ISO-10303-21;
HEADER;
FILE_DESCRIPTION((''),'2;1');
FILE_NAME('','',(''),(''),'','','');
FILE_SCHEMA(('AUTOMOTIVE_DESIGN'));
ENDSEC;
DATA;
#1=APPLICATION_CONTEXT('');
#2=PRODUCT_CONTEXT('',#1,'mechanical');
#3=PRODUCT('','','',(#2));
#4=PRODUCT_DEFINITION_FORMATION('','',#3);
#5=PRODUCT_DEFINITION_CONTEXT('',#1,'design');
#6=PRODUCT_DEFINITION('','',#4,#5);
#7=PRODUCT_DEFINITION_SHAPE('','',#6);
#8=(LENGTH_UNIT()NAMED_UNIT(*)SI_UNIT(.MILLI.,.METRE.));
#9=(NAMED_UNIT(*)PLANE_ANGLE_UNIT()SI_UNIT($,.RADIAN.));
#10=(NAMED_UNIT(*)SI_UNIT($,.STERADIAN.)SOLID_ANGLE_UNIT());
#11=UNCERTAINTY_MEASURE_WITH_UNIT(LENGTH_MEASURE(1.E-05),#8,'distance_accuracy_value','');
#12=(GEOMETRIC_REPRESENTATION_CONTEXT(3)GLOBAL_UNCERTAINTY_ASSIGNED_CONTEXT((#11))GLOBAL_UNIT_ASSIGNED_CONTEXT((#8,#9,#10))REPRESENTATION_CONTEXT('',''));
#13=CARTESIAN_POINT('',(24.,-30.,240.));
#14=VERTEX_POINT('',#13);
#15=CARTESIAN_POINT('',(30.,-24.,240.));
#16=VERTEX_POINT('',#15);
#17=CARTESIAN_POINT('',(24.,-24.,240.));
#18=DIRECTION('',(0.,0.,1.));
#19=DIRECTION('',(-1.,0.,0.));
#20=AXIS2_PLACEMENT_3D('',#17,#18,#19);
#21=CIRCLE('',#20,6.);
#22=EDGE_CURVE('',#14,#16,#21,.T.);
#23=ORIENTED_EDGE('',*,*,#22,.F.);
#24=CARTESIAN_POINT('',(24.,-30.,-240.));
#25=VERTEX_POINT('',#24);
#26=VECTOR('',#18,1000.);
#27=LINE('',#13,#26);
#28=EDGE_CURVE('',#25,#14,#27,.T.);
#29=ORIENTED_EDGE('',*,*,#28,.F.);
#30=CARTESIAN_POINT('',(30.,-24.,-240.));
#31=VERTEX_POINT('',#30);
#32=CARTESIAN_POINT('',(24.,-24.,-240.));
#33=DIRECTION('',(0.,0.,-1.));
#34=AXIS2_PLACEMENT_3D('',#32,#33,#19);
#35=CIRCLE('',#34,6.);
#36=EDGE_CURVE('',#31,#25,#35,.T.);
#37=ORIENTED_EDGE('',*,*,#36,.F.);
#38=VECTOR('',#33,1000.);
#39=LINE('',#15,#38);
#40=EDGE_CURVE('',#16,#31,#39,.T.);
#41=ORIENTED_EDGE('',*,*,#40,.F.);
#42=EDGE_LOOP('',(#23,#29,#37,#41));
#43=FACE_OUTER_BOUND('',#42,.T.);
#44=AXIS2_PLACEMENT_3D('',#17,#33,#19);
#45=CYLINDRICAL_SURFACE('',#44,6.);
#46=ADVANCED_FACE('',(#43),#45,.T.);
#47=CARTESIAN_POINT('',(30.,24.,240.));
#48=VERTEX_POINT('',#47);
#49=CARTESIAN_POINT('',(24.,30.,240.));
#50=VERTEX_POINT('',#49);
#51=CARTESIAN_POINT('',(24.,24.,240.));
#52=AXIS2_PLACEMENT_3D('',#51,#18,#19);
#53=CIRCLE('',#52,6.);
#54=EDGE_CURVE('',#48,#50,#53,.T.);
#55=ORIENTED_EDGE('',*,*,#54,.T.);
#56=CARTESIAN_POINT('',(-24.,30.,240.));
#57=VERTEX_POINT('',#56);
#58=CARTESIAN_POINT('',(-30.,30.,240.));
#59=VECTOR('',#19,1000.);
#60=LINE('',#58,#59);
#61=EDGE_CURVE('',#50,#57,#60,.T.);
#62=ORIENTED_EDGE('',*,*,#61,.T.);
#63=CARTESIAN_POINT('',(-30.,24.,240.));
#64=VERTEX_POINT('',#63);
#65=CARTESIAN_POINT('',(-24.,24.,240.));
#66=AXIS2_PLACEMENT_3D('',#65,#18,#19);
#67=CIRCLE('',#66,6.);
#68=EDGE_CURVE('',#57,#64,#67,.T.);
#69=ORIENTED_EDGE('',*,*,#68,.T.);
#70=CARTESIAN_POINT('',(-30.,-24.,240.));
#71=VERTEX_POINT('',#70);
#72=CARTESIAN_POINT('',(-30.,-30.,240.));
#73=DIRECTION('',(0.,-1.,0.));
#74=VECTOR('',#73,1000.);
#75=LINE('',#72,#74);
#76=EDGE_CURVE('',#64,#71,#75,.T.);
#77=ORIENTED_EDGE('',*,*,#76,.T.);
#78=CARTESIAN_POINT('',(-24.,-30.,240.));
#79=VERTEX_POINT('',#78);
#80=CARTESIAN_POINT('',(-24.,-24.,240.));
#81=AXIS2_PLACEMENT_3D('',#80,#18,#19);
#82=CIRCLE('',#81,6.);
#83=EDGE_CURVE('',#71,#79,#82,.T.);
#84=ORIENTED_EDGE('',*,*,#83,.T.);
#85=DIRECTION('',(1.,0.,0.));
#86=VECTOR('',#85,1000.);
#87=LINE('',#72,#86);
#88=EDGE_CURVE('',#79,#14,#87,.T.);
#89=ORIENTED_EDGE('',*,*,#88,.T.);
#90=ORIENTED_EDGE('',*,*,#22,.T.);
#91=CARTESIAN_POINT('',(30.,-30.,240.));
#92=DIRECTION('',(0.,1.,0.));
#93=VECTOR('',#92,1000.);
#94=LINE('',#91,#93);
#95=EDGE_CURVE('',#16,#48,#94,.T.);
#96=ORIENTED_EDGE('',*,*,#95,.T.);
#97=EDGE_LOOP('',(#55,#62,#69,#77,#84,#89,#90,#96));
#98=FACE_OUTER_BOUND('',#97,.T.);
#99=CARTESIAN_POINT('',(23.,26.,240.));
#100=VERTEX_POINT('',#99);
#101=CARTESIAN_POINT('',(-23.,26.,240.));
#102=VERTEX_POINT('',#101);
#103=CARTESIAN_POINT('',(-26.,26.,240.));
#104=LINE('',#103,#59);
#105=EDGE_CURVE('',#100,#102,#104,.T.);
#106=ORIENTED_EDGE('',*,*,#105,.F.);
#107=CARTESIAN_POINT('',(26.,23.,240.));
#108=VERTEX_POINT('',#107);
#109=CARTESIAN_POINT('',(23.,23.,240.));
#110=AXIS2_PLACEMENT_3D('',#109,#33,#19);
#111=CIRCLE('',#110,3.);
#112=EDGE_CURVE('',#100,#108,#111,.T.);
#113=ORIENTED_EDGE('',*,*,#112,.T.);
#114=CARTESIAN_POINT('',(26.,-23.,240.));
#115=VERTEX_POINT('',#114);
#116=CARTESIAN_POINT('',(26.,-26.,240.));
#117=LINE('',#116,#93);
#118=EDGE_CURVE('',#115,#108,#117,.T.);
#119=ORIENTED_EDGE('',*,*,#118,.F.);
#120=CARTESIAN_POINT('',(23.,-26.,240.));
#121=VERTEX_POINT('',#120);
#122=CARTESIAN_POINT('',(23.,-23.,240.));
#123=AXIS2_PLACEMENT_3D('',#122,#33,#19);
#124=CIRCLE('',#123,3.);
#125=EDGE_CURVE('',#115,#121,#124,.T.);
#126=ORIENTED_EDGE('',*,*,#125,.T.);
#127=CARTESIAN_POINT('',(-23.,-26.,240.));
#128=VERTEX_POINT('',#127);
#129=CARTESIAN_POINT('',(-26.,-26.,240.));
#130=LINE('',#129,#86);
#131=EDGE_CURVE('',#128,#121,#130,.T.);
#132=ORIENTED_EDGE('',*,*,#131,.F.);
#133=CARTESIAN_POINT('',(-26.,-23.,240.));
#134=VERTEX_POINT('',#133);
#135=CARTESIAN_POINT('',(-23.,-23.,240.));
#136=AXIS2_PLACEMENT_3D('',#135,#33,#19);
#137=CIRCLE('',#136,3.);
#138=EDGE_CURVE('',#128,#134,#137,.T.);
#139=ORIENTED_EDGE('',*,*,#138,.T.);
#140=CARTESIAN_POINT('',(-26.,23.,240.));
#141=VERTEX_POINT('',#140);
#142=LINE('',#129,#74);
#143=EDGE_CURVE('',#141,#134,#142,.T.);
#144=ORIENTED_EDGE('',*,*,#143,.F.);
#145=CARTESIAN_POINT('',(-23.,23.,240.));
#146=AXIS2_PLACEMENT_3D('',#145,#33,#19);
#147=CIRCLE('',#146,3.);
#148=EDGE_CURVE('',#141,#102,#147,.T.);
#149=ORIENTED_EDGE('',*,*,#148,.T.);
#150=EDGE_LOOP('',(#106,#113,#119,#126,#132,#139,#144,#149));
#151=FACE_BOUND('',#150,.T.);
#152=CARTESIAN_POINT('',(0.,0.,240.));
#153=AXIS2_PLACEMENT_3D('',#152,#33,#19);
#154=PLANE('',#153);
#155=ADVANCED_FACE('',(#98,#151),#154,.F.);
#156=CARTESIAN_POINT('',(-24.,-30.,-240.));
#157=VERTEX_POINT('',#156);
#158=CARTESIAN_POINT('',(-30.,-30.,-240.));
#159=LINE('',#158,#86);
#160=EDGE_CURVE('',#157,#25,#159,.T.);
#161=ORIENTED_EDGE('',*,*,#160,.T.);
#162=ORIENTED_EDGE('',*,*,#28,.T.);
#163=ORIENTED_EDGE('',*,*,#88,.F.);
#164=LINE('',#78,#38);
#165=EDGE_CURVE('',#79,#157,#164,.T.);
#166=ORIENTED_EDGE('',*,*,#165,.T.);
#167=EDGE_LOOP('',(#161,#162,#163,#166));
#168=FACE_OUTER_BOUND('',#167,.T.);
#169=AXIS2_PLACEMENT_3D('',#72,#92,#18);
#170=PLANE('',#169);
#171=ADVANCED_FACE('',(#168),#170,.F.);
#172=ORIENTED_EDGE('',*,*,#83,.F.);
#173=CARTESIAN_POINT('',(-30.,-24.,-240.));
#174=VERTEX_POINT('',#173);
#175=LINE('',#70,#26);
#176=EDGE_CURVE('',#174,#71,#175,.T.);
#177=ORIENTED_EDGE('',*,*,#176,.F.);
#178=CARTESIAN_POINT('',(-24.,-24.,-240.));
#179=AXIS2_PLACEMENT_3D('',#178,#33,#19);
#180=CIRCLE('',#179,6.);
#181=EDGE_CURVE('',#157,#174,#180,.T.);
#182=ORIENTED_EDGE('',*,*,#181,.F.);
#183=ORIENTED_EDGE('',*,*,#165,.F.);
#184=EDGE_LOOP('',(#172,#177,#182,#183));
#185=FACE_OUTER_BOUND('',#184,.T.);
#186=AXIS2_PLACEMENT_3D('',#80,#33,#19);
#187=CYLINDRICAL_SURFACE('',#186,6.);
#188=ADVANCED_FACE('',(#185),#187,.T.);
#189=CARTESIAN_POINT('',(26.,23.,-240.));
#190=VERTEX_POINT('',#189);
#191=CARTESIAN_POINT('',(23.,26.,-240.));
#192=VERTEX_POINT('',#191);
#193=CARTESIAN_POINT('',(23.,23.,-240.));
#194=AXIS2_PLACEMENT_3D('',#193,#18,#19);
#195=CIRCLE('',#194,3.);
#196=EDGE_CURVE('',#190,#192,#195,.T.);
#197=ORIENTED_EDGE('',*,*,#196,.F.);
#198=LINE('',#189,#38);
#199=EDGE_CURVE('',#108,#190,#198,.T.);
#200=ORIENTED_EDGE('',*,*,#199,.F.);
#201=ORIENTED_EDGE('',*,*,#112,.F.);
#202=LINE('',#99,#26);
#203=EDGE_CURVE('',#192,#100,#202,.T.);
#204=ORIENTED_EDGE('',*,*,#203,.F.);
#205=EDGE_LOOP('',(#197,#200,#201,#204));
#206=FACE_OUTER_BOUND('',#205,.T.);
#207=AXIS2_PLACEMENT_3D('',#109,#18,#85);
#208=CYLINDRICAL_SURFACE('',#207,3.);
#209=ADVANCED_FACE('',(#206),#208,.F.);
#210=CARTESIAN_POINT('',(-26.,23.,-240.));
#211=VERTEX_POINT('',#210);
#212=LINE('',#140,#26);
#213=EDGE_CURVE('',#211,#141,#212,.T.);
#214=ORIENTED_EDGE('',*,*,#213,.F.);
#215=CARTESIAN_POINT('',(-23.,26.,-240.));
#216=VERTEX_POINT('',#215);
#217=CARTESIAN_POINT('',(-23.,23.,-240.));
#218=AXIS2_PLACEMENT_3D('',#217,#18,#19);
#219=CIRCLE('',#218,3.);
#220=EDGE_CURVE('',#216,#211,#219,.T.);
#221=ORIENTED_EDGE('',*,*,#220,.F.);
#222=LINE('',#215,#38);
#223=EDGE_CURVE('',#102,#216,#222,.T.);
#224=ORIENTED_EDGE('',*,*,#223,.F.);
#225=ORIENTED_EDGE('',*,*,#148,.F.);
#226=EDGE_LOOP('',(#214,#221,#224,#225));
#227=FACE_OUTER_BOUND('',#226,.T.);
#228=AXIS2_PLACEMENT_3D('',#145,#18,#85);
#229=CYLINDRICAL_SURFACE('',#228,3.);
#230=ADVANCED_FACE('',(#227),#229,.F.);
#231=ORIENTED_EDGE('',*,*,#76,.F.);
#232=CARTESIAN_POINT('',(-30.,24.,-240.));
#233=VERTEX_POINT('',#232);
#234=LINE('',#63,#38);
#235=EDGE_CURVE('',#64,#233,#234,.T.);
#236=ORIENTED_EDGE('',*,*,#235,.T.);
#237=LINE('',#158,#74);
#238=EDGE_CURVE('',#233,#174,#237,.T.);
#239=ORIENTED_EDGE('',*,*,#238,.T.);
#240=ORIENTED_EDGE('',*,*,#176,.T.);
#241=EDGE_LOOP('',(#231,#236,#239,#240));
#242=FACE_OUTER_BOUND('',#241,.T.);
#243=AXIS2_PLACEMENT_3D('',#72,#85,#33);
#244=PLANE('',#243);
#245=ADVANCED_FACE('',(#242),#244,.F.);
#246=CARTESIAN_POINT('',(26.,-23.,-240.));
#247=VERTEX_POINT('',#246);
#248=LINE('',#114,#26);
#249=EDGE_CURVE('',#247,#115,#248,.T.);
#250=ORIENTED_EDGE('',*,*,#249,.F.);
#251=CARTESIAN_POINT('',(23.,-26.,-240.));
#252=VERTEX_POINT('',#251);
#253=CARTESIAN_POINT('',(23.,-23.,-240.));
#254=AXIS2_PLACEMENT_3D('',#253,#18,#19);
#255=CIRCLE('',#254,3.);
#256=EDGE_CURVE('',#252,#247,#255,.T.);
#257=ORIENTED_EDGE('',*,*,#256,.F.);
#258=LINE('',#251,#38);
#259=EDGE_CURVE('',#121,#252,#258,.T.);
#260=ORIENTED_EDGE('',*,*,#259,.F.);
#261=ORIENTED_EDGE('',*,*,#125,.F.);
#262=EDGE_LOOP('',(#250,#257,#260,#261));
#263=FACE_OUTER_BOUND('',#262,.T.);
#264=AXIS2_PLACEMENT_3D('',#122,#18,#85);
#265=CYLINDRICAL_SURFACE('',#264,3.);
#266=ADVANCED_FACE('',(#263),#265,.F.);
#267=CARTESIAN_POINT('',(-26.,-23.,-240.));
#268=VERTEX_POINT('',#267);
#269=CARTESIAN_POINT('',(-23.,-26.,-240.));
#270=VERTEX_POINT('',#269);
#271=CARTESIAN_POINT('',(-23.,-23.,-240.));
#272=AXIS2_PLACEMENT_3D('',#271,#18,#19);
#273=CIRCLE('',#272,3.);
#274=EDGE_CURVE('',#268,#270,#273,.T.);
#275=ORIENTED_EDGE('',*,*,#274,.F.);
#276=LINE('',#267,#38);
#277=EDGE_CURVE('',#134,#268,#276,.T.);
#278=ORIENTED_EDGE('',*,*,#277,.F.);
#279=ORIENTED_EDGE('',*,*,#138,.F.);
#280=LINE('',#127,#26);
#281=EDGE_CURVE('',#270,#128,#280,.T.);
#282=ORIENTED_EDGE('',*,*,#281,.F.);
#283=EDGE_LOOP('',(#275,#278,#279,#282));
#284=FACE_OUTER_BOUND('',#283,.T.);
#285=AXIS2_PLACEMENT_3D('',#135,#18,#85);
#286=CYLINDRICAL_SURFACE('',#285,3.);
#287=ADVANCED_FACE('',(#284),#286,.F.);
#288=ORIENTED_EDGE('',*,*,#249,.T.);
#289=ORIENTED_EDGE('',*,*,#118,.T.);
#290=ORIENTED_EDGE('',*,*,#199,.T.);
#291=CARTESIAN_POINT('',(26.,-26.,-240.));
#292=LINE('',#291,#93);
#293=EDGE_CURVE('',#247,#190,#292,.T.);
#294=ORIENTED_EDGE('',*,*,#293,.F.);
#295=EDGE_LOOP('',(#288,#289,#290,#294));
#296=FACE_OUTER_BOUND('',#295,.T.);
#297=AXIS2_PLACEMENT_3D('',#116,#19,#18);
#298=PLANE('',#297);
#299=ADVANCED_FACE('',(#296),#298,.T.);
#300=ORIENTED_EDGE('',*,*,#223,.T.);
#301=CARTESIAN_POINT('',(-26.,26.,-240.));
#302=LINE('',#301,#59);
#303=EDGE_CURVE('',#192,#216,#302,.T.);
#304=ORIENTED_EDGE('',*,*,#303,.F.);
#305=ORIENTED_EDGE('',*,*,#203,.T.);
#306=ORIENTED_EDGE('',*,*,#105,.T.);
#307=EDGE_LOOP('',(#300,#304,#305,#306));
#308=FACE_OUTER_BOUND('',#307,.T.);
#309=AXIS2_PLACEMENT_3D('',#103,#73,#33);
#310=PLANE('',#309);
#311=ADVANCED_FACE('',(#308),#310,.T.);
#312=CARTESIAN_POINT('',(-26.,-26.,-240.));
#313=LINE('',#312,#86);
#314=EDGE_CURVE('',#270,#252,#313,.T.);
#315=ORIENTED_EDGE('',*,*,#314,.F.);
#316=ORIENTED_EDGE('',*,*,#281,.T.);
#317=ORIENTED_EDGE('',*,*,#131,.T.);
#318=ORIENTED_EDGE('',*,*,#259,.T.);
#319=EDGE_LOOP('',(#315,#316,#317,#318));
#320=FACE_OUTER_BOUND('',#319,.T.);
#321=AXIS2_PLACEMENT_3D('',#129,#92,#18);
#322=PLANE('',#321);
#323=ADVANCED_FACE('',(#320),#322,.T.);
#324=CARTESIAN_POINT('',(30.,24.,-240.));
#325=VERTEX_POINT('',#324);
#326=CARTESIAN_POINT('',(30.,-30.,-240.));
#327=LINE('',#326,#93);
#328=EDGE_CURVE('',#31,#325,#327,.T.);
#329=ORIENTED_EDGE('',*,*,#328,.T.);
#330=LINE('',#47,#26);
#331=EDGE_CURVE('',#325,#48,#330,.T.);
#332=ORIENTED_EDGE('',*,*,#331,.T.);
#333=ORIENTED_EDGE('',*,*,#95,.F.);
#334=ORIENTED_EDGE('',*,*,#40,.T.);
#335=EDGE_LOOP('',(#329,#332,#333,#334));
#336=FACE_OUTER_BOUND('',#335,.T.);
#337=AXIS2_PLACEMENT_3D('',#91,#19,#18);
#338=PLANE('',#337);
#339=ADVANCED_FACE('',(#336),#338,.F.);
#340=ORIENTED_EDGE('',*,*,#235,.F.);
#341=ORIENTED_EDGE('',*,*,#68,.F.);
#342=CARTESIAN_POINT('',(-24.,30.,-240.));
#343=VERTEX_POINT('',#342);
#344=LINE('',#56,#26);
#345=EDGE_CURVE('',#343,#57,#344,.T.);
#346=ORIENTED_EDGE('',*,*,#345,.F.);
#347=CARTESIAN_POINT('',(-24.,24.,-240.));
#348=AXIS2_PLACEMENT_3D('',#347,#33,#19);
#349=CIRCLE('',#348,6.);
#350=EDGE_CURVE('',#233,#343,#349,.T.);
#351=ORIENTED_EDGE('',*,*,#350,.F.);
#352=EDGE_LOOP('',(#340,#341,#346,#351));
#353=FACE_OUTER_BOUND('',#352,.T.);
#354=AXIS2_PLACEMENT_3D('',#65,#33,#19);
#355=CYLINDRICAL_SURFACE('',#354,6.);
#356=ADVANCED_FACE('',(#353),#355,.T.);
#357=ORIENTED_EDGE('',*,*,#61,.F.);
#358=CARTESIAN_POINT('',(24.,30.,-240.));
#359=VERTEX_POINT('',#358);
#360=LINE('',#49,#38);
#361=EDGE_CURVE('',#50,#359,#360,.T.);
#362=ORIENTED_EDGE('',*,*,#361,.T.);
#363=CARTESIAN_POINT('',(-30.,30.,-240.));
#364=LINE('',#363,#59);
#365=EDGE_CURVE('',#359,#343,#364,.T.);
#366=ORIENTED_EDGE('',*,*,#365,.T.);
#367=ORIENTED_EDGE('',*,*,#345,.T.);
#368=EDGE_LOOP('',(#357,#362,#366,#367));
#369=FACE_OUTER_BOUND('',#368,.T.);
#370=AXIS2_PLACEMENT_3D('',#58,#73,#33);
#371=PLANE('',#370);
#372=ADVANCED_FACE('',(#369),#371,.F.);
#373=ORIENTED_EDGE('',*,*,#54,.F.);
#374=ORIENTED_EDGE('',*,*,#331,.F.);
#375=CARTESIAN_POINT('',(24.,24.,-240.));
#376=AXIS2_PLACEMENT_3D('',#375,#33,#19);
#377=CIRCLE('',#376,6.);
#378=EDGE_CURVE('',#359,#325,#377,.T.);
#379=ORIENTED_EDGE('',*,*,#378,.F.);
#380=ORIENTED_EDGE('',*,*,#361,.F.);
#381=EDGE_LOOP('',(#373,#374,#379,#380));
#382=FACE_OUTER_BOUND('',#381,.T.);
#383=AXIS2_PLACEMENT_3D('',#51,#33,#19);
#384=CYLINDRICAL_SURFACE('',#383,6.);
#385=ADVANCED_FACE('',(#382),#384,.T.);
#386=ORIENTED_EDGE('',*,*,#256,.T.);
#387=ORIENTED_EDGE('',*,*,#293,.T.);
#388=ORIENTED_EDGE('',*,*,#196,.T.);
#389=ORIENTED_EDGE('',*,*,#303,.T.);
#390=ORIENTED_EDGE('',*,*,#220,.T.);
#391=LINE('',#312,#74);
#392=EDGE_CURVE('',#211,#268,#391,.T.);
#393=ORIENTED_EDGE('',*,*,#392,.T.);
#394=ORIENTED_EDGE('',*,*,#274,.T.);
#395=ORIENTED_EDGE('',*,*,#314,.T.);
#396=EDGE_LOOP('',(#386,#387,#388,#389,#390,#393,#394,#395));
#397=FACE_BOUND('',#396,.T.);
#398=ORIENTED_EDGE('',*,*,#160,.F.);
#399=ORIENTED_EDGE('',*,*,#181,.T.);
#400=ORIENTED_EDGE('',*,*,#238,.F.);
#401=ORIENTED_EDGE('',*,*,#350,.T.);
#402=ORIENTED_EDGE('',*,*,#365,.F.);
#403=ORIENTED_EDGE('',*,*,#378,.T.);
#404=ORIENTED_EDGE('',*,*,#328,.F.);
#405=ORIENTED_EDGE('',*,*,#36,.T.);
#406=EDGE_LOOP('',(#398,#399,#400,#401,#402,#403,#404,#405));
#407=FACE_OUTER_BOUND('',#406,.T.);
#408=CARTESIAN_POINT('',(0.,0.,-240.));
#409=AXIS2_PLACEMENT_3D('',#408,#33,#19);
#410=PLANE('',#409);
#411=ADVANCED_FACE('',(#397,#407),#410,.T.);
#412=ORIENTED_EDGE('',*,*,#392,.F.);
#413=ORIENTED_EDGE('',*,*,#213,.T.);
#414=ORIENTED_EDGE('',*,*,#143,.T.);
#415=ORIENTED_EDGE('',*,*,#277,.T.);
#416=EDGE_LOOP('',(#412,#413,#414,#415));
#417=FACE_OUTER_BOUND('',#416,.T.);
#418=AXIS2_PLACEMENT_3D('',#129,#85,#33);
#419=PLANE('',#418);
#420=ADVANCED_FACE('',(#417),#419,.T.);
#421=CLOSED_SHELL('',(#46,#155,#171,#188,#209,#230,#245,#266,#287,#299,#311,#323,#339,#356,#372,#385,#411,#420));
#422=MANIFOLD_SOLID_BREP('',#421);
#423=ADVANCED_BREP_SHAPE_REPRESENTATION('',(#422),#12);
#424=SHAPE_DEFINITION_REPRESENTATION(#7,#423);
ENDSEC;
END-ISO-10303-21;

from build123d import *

# Parameters (mm, degrees)
SKETCH1_W           = 60
SKETCH1_H           = 60
SKETCH1_W_2         = 52
SKETCH1_H_2         = 52
BOSS_EXTRUDE1_DEPTH = 240
FILLET1_R           = 6
FILLET2_R           = 3


with BuildPart() as part:
    # Sketch1 → Boss-Extrude1 (new, symmetric)
    with BuildSketch(Plane.XY):
        Rectangle(SKETCH1_W, SKETCH1_H)
        Rectangle(SKETCH1_W_2, SKETCH1_H_2, mode=Mode.SUBTRACT)
    extrude(amount=BOSS_EXTRUDE1_DEPTH, both=True)

    # Fillet1
    fillet1_edges = [part.edges().sort_by_distance(p)[0] for p in [
        (30, -30, 0),
        (-30, -30, 0),
        (-30, 30, 0),
        (30, 30, 0),
    ]]
    fillet(fillet1_edges, radius=FILLET1_R)

    # Fillet2
    fillet2_edges = [part.edges().sort_by_distance(p)[0] for p in [
        (26, -26, 0),
        (26, 26, 0),
        (-26, 26, 0),
        (-26, -26, 0),
    ]]
    fillet(fillet2_edges, radius=FILLET2_R)


solid = part.part
